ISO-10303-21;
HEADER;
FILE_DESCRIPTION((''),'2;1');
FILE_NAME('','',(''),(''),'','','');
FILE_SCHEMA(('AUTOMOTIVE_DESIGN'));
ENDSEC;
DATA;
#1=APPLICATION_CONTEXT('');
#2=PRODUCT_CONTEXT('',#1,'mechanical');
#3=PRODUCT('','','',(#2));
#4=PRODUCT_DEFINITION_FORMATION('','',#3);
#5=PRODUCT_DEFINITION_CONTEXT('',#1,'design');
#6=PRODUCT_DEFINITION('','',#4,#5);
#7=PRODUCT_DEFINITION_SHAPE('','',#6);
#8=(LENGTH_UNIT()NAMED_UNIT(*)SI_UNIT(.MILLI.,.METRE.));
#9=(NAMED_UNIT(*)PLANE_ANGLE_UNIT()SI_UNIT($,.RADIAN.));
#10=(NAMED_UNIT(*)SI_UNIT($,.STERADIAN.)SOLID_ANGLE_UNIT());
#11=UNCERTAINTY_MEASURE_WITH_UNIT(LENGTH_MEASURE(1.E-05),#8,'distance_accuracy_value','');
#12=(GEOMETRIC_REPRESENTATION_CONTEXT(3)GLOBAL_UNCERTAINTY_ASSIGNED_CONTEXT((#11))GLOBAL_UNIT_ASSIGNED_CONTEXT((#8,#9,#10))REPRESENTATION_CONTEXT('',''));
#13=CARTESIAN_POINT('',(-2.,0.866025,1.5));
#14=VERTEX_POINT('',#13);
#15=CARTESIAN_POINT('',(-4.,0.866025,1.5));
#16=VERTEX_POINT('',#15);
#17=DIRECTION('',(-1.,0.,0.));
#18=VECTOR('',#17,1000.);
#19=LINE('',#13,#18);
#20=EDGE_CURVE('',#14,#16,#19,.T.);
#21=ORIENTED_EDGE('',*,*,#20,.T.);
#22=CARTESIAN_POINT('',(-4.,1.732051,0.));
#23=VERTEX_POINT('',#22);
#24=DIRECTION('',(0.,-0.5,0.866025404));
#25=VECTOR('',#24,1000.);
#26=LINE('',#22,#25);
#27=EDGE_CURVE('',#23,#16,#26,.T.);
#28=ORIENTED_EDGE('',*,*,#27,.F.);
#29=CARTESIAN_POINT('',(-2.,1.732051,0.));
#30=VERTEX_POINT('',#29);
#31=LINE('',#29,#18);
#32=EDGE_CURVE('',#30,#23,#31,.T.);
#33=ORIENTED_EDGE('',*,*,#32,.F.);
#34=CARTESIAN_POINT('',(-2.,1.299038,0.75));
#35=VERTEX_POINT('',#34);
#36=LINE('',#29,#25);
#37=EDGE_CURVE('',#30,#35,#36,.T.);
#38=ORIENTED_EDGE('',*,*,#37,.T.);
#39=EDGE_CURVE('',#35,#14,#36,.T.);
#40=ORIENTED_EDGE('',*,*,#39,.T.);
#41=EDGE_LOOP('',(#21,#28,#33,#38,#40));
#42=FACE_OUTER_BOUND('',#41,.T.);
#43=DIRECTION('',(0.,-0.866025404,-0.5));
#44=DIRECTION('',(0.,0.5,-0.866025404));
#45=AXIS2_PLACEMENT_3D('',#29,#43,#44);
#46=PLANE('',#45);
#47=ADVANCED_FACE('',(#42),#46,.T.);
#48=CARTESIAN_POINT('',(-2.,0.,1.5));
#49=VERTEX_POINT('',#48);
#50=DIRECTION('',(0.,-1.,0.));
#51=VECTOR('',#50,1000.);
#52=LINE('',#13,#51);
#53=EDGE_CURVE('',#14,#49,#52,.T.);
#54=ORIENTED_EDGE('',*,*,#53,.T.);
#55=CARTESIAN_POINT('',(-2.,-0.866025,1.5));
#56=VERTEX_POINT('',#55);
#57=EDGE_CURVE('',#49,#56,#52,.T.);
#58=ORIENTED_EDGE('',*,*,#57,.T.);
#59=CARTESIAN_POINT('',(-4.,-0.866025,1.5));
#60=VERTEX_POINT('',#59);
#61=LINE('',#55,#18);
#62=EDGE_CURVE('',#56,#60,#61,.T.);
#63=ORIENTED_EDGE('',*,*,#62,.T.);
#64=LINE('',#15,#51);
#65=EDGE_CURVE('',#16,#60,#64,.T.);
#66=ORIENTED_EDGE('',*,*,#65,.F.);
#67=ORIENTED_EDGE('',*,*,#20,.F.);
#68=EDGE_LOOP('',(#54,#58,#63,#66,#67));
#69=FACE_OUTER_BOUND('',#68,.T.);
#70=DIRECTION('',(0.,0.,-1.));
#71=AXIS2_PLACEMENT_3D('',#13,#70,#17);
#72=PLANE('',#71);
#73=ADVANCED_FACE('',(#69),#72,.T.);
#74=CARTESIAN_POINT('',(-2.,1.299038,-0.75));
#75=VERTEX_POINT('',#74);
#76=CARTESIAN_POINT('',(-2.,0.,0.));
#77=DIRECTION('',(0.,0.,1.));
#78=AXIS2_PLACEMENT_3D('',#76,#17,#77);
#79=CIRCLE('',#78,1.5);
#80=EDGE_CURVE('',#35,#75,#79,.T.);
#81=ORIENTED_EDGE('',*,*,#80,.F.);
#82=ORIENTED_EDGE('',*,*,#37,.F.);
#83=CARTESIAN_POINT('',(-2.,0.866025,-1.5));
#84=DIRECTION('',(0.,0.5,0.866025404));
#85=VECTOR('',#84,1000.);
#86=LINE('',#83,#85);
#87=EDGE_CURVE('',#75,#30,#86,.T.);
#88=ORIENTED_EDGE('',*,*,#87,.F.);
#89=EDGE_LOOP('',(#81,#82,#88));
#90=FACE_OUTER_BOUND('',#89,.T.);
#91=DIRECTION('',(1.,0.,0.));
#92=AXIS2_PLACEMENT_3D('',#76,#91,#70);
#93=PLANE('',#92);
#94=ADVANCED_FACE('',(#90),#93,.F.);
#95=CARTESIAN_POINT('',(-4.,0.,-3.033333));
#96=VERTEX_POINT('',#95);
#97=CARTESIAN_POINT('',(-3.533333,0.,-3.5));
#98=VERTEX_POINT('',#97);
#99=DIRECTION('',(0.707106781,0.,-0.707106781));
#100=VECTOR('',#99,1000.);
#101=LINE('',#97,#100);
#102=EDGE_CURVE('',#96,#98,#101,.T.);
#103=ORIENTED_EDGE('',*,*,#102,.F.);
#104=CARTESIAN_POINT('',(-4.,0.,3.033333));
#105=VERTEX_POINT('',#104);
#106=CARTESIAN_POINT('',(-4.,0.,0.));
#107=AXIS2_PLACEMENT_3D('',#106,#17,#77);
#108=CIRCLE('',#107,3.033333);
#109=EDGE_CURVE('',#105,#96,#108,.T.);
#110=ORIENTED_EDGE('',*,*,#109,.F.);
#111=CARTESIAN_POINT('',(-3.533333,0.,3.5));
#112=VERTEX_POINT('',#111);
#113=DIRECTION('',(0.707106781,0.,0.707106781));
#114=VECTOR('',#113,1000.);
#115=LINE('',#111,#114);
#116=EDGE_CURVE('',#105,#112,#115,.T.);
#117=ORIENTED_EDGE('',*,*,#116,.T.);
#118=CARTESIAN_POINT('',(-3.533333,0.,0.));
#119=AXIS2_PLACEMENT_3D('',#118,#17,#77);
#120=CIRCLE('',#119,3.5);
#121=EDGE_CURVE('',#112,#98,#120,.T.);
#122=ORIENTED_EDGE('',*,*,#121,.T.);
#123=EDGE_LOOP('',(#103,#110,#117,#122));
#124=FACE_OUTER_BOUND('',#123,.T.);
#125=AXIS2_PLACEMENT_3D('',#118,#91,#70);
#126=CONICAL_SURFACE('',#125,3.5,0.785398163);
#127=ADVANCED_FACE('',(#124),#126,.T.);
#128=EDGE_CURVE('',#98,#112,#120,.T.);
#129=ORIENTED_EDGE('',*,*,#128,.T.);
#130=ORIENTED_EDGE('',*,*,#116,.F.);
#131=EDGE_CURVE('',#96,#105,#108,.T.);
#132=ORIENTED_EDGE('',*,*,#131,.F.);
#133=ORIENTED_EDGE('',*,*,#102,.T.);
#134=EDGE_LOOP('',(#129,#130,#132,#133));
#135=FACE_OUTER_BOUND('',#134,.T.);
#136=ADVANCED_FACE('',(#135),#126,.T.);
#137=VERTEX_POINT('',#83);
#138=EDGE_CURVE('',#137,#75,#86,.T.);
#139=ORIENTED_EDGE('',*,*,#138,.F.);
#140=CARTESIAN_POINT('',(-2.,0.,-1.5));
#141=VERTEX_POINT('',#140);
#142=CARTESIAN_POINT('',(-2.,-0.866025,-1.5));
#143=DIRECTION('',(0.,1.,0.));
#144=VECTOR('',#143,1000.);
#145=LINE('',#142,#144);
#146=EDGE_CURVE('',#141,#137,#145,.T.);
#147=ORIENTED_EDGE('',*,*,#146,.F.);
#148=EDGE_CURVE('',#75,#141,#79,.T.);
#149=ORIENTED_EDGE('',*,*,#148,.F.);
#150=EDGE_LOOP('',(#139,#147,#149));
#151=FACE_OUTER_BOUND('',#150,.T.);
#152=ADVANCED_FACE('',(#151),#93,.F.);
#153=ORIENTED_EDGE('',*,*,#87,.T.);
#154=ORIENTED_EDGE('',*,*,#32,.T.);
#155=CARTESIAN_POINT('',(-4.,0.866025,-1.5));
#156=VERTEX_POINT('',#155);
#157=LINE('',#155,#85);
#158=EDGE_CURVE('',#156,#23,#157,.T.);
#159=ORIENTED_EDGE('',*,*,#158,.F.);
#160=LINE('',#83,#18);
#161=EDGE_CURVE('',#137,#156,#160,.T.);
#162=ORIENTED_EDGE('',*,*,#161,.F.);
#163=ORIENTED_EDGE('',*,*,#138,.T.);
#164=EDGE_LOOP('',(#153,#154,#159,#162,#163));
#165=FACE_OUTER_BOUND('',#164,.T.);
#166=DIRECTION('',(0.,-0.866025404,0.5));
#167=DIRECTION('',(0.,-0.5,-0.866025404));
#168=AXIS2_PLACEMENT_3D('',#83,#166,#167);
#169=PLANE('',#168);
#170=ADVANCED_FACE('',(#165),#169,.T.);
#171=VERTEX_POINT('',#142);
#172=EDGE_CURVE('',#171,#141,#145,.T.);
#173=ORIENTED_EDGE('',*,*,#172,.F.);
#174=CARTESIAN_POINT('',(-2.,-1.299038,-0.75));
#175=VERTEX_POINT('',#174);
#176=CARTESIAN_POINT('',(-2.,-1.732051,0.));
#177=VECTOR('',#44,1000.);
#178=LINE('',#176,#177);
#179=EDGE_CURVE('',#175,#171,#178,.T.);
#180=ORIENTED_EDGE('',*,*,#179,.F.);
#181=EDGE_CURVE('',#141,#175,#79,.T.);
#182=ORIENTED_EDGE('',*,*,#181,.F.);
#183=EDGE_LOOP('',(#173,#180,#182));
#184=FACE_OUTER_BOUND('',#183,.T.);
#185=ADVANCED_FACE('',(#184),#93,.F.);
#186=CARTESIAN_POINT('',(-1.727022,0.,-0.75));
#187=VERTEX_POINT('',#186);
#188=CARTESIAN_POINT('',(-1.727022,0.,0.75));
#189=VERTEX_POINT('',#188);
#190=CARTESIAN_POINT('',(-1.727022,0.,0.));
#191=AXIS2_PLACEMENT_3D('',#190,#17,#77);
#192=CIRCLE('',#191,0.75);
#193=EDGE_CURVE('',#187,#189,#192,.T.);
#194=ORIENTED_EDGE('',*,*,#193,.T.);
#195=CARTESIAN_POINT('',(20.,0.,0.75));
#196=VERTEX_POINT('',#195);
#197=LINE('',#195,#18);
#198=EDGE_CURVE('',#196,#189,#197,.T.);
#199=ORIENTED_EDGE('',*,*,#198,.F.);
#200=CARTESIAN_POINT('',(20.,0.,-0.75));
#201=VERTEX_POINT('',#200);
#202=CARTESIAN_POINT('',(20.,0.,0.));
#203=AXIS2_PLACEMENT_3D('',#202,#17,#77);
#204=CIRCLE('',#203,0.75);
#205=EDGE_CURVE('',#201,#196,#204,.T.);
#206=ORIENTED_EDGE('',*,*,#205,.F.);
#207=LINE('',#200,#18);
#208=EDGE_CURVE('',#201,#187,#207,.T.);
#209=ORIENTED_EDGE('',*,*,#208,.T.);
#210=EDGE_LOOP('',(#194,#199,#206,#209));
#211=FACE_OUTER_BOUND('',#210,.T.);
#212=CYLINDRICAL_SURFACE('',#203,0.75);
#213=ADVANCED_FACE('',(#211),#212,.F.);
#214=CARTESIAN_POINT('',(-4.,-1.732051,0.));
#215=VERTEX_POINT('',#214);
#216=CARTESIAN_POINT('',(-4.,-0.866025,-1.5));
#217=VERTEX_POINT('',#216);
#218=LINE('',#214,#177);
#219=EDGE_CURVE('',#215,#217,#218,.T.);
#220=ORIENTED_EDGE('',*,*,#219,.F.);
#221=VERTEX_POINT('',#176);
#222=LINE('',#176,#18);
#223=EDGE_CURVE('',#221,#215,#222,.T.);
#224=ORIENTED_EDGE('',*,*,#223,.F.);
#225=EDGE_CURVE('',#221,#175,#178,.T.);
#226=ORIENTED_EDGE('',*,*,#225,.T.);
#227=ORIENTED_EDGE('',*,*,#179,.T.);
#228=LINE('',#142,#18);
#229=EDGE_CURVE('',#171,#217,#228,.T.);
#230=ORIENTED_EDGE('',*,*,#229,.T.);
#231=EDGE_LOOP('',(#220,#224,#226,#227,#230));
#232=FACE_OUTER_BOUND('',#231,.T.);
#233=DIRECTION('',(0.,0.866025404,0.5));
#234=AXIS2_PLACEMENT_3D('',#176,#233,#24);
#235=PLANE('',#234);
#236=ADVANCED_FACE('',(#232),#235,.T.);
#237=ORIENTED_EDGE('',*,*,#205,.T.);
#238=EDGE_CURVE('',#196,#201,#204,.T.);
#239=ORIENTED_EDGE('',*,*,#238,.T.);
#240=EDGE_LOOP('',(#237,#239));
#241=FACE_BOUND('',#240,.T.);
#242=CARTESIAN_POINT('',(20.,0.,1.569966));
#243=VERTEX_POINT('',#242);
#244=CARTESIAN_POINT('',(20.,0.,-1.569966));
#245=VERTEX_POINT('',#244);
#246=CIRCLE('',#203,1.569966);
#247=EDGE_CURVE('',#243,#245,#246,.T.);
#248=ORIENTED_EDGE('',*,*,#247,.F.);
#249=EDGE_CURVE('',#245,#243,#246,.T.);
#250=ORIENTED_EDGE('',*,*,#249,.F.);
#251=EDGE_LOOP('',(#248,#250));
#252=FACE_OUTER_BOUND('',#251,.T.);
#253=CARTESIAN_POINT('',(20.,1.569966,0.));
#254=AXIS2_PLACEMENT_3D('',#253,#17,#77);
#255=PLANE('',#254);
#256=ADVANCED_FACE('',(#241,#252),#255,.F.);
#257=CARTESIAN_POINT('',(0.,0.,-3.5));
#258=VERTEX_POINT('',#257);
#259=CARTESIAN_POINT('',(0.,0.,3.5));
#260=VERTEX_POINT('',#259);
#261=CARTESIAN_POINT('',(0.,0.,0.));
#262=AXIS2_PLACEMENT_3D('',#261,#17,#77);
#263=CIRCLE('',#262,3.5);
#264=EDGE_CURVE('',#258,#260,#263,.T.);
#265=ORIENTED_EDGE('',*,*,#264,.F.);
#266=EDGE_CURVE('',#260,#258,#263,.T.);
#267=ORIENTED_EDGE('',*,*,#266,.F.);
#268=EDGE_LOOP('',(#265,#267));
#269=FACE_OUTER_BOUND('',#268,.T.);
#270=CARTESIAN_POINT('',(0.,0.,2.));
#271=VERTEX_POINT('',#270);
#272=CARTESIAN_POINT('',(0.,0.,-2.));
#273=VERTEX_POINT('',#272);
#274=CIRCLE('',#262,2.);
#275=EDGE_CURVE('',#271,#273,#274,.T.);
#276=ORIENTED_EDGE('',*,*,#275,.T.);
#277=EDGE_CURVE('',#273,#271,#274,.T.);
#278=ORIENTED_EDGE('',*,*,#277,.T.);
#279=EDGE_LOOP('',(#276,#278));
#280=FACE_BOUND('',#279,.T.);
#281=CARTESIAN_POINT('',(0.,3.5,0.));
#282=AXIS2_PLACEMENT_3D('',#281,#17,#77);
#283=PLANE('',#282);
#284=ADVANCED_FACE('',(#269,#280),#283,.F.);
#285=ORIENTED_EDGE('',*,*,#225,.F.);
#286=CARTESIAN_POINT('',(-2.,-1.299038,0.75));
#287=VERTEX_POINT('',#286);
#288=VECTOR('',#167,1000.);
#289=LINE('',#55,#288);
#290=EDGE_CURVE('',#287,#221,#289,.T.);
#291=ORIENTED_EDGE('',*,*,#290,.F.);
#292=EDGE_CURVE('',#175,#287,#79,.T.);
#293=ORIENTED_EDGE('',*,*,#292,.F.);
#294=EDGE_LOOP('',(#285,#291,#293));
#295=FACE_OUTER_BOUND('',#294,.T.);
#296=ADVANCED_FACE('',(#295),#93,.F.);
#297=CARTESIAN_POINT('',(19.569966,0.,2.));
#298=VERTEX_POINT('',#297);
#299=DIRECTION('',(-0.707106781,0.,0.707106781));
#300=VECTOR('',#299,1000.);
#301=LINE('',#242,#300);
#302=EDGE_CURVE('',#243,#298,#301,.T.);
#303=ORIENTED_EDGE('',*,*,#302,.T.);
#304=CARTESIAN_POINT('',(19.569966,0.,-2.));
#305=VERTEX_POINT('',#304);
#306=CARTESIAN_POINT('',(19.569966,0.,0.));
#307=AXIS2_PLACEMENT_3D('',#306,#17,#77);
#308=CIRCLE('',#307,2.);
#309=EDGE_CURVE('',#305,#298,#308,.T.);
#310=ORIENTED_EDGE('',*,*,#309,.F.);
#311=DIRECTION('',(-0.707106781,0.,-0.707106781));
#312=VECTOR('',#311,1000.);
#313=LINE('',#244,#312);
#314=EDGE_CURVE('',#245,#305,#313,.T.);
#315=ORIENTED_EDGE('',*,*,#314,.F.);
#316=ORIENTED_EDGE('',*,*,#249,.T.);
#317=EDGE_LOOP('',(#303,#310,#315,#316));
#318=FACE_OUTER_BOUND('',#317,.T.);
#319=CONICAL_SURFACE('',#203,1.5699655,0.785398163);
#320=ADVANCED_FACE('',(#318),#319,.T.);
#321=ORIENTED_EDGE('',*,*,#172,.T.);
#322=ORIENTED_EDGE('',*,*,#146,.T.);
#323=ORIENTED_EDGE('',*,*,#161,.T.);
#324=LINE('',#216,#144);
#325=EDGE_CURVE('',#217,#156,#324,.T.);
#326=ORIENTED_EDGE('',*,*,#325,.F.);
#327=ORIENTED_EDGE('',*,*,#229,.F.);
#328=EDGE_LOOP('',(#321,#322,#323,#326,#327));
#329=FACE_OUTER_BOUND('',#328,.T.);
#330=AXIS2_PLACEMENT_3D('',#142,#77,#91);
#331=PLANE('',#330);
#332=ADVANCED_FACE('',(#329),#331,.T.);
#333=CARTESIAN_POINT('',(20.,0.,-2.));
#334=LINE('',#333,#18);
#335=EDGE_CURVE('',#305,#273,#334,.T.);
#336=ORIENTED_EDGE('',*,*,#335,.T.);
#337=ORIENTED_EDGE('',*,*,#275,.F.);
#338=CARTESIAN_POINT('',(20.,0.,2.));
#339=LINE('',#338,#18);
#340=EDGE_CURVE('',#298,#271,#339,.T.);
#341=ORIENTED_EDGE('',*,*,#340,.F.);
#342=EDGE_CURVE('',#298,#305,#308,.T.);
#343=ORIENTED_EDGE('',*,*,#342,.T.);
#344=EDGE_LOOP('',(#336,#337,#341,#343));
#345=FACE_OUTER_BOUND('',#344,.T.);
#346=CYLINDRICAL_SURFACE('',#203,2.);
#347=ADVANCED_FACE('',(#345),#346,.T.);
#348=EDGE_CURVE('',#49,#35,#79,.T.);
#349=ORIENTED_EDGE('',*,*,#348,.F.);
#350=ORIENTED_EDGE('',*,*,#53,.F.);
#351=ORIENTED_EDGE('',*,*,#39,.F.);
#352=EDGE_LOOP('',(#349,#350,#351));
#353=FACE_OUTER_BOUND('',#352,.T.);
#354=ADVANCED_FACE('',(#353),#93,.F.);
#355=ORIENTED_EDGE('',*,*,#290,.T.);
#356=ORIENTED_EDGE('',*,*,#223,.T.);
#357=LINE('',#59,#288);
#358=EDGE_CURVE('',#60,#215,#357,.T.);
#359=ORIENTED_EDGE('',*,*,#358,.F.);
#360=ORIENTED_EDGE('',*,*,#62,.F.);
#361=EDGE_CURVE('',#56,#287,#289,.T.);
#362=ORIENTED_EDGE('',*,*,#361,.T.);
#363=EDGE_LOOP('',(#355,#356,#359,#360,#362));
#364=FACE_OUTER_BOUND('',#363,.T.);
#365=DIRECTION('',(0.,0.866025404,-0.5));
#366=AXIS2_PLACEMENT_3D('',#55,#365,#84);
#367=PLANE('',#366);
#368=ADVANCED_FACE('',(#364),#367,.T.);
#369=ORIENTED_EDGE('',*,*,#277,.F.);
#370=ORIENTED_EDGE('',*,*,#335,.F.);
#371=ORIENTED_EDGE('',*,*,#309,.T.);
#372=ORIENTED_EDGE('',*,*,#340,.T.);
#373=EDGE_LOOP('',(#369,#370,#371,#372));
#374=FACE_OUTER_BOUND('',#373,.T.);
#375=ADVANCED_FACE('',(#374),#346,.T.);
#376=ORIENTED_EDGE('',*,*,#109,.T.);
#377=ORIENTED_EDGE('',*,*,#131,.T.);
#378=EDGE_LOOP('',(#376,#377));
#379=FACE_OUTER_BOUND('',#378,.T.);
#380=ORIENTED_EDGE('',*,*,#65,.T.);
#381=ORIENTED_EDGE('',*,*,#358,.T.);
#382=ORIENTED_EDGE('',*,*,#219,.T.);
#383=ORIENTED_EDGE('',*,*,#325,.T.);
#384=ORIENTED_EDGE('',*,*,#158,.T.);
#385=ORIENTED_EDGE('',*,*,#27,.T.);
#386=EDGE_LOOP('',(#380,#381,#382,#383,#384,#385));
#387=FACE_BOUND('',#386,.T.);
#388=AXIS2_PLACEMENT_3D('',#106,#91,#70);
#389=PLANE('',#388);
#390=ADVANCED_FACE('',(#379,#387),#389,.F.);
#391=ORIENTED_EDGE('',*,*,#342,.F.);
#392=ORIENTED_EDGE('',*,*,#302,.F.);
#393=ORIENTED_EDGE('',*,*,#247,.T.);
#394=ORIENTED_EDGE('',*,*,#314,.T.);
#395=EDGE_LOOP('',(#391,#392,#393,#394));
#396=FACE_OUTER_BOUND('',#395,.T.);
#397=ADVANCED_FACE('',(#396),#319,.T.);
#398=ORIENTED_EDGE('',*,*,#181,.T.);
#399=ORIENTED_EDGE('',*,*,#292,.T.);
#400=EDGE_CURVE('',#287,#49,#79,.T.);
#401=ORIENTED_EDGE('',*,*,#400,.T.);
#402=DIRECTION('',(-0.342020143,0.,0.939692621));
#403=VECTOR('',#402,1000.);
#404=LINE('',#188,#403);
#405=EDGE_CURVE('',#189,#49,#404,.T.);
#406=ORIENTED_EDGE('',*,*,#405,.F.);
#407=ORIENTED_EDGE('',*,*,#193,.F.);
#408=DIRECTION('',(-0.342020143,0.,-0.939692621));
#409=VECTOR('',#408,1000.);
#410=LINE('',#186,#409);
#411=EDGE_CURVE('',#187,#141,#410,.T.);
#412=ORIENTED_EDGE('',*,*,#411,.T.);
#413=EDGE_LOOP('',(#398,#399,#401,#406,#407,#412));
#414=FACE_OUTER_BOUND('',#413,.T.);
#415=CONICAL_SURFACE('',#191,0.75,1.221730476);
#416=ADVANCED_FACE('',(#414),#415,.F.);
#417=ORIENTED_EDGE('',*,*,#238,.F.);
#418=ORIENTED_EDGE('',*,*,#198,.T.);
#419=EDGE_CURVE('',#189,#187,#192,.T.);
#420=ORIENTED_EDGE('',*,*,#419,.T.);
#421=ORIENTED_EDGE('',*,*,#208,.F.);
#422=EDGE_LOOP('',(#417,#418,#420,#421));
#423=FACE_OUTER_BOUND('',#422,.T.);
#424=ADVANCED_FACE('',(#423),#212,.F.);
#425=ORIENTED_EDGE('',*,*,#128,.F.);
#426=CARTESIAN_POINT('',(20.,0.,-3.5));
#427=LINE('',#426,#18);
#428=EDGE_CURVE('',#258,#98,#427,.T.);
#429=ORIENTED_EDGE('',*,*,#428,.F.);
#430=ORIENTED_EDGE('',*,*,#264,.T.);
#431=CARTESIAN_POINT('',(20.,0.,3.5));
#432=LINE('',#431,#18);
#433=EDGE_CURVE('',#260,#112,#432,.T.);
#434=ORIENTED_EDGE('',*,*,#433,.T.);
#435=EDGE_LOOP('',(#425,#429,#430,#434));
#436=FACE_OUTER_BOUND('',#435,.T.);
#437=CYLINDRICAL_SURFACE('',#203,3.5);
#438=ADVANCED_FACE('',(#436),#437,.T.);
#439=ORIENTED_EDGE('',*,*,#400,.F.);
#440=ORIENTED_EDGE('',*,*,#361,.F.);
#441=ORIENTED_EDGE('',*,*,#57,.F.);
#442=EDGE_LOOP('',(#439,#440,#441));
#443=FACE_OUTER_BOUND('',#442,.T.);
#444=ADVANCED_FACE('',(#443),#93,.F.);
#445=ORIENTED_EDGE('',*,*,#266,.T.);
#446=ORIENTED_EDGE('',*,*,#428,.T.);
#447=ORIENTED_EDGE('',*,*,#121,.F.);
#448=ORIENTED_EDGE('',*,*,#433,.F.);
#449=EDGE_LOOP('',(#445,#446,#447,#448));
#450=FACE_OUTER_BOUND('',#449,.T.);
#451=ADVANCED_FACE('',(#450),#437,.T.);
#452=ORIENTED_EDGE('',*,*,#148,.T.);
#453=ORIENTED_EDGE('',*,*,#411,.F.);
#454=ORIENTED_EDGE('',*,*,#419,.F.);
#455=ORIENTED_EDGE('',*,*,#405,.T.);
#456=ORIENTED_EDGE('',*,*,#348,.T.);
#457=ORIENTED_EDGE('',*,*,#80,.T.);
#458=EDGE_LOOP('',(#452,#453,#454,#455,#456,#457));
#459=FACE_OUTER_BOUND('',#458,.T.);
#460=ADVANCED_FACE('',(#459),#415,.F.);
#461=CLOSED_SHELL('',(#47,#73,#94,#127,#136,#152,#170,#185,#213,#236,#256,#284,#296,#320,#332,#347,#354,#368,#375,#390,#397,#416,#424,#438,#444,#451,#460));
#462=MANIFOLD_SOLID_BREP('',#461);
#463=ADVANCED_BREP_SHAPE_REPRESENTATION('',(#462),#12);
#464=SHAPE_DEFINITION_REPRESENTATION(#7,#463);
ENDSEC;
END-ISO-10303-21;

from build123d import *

# Parameters (mm, degrees)
CUT_EXTRUDE1_DEPTH = 2


with BuildPart() as part:
    # Sketch1 → Revolve1 (revolve)
    with BuildSketch(Plane.XY, mode=Mode.PRIVATE) as revolve1_sk:
        Polygon((-4, 0), (-4, 3.033333333), (-3.533333333, 3.5), (0, 3.5), (0, 2), (19.5699655, 2), (20, 1.5699655), (20, 0), align=None)
    revolve(revolve1_sk.sketch.rotate(Axis((20, 0, 0), (-1, 0, 0)), 270), axis=Axis((20, 0, 0), (-1, 0, 0)))

    # Sketch2 → Cut-Revolve1 (revolve, cut)
    with BuildSketch(Plane.XY, mode=Mode.PRIVATE) as cut_revolve1_sk:
        Polygon((-4, 0), (-4, 1.5), (-2, 1.5), (-1.727022324, 0.75), (20, 0.75), (20, 0), align=None)
    revolve(cut_revolve1_sk.sketch.rotate(Axis((20, 0, 0), (-1, 0, 0)), 270), axis=Axis((20, 0, 0), (-1, 0, 0)), mode=Mode.SUBTRACT)

    # Sketch3 → Cut-Extrude1 (cut)
    with BuildSketch(Plane(origin=(-4, 0, 0), x_dir=(0, 0, -1), z_dir=(1, 0, 0))):
        Polygon((-1.5, 0.866025404), (-1.5, -0.866025404), (0, -1.732050808), (1.5, -0.866025404), (1.5, 0.866025404), (0, 1.732050808), align=None)
    extrude(amount=CUT_EXTRUDE1_DEPTH, mode=Mode.SUBTRACT)


solid = part.part
